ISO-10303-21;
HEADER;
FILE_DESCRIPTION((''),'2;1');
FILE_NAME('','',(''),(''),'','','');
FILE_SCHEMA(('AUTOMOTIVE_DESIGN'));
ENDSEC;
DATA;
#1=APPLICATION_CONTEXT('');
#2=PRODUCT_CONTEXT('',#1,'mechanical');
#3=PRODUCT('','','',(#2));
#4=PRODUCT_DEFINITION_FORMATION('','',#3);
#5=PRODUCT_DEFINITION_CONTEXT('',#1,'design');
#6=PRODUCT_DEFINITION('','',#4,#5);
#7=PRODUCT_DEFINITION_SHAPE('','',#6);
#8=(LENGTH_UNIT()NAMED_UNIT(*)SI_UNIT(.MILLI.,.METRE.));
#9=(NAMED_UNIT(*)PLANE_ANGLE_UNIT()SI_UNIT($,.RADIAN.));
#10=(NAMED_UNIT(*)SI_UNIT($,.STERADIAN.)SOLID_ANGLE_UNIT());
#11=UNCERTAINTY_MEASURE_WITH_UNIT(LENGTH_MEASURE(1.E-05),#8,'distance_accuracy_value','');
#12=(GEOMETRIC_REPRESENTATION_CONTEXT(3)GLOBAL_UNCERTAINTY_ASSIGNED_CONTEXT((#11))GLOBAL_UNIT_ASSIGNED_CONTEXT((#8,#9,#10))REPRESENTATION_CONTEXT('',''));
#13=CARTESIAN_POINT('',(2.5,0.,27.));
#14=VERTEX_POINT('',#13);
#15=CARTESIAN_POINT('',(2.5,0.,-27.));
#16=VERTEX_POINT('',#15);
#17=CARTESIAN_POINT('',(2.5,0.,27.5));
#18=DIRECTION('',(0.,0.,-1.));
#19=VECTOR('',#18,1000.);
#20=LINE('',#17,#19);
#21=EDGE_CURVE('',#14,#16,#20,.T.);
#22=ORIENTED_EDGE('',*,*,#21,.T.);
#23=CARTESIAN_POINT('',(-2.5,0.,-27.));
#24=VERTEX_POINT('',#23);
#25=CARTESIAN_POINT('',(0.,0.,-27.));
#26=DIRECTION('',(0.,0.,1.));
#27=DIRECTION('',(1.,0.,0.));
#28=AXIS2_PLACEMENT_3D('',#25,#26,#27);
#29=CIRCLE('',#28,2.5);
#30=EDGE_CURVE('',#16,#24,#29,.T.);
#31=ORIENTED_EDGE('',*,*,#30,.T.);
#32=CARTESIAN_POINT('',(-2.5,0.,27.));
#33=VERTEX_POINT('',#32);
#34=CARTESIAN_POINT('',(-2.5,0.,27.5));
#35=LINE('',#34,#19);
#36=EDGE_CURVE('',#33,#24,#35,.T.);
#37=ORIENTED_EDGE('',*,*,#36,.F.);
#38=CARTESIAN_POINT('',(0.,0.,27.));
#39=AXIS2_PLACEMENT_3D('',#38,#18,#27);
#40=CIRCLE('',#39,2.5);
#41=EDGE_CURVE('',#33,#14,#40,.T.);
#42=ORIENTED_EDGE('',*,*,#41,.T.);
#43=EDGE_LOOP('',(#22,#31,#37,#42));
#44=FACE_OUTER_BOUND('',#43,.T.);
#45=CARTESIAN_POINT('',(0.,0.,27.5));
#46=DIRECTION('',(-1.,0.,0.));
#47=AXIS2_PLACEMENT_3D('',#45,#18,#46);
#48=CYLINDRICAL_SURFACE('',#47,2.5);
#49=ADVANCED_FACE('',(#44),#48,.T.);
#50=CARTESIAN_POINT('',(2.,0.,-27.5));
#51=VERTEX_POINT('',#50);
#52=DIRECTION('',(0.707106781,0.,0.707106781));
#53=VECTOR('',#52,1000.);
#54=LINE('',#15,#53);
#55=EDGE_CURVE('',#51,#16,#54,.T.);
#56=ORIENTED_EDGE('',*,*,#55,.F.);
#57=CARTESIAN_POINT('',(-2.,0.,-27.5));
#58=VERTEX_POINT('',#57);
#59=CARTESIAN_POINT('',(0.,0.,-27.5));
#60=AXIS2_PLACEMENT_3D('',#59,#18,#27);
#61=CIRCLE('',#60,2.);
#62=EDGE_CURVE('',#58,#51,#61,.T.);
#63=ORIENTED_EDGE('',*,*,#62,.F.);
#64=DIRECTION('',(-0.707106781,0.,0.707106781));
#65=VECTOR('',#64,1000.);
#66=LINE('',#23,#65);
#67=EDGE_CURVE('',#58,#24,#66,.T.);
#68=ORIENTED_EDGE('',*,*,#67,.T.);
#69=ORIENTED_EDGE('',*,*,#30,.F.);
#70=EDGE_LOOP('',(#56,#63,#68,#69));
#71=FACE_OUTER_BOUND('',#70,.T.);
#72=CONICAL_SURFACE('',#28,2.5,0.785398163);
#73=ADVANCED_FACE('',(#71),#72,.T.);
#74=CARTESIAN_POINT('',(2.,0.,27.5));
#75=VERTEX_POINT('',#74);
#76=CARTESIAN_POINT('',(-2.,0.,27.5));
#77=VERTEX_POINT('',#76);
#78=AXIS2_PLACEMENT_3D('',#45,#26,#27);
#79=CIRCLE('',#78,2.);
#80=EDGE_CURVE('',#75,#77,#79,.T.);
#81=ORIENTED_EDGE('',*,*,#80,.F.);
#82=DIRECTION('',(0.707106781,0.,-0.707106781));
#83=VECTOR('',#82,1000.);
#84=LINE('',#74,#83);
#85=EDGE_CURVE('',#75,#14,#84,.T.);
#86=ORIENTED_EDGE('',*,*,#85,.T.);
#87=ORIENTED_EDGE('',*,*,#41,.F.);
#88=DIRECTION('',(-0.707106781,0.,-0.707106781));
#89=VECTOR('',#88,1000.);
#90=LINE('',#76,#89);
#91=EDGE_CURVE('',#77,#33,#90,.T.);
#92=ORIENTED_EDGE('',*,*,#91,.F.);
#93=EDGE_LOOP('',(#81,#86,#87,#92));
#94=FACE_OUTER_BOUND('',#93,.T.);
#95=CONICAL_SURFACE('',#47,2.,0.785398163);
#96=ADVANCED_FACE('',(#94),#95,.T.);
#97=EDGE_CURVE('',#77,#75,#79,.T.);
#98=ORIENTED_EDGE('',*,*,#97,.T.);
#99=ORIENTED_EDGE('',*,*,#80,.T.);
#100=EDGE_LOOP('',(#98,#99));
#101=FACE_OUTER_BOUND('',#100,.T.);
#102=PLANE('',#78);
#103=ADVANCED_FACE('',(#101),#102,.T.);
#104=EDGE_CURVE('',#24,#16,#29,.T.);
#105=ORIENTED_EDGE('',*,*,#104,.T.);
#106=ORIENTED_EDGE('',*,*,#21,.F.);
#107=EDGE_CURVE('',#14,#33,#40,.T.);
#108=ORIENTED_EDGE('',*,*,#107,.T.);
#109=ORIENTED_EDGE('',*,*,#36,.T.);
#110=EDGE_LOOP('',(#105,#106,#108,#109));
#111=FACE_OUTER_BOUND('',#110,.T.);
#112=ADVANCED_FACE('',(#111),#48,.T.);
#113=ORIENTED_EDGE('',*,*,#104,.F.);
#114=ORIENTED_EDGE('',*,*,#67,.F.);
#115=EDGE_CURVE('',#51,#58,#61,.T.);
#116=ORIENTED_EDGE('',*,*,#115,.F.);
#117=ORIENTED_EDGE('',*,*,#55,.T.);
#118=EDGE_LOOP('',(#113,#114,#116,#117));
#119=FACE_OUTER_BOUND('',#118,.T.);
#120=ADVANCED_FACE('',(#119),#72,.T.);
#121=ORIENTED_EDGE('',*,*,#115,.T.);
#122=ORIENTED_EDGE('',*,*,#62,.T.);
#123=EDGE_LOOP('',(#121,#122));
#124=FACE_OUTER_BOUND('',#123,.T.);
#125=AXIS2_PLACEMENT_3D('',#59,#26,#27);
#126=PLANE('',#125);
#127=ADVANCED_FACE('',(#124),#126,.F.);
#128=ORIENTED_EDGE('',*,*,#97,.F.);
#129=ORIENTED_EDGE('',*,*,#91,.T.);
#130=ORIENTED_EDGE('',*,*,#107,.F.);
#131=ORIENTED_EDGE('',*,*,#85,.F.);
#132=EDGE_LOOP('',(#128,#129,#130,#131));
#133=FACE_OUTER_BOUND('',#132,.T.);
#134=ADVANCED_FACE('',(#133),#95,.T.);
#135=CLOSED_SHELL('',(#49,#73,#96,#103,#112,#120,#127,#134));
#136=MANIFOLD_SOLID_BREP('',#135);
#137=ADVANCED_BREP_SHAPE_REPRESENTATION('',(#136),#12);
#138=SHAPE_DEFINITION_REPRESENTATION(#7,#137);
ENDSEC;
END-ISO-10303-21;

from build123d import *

# Parameters (mm, degrees)
PIN_PROFILE_5_R          = 2.5
PIN_BODY_5X55_DEPTH      = 27.5
END_CHAMFERS_0_5X45_SIZE = 0.5


with BuildPart() as part:
    # Pin Profile Ø5 → Pin Body Ø5x55 (new, symmetric)
    with BuildSketch(Plane.XY):
        Circle(PIN_PROFILE_5_R)
    extrude(amount=PIN_BODY_5X55_DEPTH, both=True)

    # End Chamfers 0.5x45°
    end_chamfers_0_5x45_edges = [part.edges().sort_by_distance(p)[0] for p in [
        (-2.5, 0, -27.5),
        (-2.5, 0, 27.5),
    ]]
    chamfer(end_chamfers_0_5x45_edges, length=END_CHAMFERS_0_5X45_SIZE)


solid = part.part
